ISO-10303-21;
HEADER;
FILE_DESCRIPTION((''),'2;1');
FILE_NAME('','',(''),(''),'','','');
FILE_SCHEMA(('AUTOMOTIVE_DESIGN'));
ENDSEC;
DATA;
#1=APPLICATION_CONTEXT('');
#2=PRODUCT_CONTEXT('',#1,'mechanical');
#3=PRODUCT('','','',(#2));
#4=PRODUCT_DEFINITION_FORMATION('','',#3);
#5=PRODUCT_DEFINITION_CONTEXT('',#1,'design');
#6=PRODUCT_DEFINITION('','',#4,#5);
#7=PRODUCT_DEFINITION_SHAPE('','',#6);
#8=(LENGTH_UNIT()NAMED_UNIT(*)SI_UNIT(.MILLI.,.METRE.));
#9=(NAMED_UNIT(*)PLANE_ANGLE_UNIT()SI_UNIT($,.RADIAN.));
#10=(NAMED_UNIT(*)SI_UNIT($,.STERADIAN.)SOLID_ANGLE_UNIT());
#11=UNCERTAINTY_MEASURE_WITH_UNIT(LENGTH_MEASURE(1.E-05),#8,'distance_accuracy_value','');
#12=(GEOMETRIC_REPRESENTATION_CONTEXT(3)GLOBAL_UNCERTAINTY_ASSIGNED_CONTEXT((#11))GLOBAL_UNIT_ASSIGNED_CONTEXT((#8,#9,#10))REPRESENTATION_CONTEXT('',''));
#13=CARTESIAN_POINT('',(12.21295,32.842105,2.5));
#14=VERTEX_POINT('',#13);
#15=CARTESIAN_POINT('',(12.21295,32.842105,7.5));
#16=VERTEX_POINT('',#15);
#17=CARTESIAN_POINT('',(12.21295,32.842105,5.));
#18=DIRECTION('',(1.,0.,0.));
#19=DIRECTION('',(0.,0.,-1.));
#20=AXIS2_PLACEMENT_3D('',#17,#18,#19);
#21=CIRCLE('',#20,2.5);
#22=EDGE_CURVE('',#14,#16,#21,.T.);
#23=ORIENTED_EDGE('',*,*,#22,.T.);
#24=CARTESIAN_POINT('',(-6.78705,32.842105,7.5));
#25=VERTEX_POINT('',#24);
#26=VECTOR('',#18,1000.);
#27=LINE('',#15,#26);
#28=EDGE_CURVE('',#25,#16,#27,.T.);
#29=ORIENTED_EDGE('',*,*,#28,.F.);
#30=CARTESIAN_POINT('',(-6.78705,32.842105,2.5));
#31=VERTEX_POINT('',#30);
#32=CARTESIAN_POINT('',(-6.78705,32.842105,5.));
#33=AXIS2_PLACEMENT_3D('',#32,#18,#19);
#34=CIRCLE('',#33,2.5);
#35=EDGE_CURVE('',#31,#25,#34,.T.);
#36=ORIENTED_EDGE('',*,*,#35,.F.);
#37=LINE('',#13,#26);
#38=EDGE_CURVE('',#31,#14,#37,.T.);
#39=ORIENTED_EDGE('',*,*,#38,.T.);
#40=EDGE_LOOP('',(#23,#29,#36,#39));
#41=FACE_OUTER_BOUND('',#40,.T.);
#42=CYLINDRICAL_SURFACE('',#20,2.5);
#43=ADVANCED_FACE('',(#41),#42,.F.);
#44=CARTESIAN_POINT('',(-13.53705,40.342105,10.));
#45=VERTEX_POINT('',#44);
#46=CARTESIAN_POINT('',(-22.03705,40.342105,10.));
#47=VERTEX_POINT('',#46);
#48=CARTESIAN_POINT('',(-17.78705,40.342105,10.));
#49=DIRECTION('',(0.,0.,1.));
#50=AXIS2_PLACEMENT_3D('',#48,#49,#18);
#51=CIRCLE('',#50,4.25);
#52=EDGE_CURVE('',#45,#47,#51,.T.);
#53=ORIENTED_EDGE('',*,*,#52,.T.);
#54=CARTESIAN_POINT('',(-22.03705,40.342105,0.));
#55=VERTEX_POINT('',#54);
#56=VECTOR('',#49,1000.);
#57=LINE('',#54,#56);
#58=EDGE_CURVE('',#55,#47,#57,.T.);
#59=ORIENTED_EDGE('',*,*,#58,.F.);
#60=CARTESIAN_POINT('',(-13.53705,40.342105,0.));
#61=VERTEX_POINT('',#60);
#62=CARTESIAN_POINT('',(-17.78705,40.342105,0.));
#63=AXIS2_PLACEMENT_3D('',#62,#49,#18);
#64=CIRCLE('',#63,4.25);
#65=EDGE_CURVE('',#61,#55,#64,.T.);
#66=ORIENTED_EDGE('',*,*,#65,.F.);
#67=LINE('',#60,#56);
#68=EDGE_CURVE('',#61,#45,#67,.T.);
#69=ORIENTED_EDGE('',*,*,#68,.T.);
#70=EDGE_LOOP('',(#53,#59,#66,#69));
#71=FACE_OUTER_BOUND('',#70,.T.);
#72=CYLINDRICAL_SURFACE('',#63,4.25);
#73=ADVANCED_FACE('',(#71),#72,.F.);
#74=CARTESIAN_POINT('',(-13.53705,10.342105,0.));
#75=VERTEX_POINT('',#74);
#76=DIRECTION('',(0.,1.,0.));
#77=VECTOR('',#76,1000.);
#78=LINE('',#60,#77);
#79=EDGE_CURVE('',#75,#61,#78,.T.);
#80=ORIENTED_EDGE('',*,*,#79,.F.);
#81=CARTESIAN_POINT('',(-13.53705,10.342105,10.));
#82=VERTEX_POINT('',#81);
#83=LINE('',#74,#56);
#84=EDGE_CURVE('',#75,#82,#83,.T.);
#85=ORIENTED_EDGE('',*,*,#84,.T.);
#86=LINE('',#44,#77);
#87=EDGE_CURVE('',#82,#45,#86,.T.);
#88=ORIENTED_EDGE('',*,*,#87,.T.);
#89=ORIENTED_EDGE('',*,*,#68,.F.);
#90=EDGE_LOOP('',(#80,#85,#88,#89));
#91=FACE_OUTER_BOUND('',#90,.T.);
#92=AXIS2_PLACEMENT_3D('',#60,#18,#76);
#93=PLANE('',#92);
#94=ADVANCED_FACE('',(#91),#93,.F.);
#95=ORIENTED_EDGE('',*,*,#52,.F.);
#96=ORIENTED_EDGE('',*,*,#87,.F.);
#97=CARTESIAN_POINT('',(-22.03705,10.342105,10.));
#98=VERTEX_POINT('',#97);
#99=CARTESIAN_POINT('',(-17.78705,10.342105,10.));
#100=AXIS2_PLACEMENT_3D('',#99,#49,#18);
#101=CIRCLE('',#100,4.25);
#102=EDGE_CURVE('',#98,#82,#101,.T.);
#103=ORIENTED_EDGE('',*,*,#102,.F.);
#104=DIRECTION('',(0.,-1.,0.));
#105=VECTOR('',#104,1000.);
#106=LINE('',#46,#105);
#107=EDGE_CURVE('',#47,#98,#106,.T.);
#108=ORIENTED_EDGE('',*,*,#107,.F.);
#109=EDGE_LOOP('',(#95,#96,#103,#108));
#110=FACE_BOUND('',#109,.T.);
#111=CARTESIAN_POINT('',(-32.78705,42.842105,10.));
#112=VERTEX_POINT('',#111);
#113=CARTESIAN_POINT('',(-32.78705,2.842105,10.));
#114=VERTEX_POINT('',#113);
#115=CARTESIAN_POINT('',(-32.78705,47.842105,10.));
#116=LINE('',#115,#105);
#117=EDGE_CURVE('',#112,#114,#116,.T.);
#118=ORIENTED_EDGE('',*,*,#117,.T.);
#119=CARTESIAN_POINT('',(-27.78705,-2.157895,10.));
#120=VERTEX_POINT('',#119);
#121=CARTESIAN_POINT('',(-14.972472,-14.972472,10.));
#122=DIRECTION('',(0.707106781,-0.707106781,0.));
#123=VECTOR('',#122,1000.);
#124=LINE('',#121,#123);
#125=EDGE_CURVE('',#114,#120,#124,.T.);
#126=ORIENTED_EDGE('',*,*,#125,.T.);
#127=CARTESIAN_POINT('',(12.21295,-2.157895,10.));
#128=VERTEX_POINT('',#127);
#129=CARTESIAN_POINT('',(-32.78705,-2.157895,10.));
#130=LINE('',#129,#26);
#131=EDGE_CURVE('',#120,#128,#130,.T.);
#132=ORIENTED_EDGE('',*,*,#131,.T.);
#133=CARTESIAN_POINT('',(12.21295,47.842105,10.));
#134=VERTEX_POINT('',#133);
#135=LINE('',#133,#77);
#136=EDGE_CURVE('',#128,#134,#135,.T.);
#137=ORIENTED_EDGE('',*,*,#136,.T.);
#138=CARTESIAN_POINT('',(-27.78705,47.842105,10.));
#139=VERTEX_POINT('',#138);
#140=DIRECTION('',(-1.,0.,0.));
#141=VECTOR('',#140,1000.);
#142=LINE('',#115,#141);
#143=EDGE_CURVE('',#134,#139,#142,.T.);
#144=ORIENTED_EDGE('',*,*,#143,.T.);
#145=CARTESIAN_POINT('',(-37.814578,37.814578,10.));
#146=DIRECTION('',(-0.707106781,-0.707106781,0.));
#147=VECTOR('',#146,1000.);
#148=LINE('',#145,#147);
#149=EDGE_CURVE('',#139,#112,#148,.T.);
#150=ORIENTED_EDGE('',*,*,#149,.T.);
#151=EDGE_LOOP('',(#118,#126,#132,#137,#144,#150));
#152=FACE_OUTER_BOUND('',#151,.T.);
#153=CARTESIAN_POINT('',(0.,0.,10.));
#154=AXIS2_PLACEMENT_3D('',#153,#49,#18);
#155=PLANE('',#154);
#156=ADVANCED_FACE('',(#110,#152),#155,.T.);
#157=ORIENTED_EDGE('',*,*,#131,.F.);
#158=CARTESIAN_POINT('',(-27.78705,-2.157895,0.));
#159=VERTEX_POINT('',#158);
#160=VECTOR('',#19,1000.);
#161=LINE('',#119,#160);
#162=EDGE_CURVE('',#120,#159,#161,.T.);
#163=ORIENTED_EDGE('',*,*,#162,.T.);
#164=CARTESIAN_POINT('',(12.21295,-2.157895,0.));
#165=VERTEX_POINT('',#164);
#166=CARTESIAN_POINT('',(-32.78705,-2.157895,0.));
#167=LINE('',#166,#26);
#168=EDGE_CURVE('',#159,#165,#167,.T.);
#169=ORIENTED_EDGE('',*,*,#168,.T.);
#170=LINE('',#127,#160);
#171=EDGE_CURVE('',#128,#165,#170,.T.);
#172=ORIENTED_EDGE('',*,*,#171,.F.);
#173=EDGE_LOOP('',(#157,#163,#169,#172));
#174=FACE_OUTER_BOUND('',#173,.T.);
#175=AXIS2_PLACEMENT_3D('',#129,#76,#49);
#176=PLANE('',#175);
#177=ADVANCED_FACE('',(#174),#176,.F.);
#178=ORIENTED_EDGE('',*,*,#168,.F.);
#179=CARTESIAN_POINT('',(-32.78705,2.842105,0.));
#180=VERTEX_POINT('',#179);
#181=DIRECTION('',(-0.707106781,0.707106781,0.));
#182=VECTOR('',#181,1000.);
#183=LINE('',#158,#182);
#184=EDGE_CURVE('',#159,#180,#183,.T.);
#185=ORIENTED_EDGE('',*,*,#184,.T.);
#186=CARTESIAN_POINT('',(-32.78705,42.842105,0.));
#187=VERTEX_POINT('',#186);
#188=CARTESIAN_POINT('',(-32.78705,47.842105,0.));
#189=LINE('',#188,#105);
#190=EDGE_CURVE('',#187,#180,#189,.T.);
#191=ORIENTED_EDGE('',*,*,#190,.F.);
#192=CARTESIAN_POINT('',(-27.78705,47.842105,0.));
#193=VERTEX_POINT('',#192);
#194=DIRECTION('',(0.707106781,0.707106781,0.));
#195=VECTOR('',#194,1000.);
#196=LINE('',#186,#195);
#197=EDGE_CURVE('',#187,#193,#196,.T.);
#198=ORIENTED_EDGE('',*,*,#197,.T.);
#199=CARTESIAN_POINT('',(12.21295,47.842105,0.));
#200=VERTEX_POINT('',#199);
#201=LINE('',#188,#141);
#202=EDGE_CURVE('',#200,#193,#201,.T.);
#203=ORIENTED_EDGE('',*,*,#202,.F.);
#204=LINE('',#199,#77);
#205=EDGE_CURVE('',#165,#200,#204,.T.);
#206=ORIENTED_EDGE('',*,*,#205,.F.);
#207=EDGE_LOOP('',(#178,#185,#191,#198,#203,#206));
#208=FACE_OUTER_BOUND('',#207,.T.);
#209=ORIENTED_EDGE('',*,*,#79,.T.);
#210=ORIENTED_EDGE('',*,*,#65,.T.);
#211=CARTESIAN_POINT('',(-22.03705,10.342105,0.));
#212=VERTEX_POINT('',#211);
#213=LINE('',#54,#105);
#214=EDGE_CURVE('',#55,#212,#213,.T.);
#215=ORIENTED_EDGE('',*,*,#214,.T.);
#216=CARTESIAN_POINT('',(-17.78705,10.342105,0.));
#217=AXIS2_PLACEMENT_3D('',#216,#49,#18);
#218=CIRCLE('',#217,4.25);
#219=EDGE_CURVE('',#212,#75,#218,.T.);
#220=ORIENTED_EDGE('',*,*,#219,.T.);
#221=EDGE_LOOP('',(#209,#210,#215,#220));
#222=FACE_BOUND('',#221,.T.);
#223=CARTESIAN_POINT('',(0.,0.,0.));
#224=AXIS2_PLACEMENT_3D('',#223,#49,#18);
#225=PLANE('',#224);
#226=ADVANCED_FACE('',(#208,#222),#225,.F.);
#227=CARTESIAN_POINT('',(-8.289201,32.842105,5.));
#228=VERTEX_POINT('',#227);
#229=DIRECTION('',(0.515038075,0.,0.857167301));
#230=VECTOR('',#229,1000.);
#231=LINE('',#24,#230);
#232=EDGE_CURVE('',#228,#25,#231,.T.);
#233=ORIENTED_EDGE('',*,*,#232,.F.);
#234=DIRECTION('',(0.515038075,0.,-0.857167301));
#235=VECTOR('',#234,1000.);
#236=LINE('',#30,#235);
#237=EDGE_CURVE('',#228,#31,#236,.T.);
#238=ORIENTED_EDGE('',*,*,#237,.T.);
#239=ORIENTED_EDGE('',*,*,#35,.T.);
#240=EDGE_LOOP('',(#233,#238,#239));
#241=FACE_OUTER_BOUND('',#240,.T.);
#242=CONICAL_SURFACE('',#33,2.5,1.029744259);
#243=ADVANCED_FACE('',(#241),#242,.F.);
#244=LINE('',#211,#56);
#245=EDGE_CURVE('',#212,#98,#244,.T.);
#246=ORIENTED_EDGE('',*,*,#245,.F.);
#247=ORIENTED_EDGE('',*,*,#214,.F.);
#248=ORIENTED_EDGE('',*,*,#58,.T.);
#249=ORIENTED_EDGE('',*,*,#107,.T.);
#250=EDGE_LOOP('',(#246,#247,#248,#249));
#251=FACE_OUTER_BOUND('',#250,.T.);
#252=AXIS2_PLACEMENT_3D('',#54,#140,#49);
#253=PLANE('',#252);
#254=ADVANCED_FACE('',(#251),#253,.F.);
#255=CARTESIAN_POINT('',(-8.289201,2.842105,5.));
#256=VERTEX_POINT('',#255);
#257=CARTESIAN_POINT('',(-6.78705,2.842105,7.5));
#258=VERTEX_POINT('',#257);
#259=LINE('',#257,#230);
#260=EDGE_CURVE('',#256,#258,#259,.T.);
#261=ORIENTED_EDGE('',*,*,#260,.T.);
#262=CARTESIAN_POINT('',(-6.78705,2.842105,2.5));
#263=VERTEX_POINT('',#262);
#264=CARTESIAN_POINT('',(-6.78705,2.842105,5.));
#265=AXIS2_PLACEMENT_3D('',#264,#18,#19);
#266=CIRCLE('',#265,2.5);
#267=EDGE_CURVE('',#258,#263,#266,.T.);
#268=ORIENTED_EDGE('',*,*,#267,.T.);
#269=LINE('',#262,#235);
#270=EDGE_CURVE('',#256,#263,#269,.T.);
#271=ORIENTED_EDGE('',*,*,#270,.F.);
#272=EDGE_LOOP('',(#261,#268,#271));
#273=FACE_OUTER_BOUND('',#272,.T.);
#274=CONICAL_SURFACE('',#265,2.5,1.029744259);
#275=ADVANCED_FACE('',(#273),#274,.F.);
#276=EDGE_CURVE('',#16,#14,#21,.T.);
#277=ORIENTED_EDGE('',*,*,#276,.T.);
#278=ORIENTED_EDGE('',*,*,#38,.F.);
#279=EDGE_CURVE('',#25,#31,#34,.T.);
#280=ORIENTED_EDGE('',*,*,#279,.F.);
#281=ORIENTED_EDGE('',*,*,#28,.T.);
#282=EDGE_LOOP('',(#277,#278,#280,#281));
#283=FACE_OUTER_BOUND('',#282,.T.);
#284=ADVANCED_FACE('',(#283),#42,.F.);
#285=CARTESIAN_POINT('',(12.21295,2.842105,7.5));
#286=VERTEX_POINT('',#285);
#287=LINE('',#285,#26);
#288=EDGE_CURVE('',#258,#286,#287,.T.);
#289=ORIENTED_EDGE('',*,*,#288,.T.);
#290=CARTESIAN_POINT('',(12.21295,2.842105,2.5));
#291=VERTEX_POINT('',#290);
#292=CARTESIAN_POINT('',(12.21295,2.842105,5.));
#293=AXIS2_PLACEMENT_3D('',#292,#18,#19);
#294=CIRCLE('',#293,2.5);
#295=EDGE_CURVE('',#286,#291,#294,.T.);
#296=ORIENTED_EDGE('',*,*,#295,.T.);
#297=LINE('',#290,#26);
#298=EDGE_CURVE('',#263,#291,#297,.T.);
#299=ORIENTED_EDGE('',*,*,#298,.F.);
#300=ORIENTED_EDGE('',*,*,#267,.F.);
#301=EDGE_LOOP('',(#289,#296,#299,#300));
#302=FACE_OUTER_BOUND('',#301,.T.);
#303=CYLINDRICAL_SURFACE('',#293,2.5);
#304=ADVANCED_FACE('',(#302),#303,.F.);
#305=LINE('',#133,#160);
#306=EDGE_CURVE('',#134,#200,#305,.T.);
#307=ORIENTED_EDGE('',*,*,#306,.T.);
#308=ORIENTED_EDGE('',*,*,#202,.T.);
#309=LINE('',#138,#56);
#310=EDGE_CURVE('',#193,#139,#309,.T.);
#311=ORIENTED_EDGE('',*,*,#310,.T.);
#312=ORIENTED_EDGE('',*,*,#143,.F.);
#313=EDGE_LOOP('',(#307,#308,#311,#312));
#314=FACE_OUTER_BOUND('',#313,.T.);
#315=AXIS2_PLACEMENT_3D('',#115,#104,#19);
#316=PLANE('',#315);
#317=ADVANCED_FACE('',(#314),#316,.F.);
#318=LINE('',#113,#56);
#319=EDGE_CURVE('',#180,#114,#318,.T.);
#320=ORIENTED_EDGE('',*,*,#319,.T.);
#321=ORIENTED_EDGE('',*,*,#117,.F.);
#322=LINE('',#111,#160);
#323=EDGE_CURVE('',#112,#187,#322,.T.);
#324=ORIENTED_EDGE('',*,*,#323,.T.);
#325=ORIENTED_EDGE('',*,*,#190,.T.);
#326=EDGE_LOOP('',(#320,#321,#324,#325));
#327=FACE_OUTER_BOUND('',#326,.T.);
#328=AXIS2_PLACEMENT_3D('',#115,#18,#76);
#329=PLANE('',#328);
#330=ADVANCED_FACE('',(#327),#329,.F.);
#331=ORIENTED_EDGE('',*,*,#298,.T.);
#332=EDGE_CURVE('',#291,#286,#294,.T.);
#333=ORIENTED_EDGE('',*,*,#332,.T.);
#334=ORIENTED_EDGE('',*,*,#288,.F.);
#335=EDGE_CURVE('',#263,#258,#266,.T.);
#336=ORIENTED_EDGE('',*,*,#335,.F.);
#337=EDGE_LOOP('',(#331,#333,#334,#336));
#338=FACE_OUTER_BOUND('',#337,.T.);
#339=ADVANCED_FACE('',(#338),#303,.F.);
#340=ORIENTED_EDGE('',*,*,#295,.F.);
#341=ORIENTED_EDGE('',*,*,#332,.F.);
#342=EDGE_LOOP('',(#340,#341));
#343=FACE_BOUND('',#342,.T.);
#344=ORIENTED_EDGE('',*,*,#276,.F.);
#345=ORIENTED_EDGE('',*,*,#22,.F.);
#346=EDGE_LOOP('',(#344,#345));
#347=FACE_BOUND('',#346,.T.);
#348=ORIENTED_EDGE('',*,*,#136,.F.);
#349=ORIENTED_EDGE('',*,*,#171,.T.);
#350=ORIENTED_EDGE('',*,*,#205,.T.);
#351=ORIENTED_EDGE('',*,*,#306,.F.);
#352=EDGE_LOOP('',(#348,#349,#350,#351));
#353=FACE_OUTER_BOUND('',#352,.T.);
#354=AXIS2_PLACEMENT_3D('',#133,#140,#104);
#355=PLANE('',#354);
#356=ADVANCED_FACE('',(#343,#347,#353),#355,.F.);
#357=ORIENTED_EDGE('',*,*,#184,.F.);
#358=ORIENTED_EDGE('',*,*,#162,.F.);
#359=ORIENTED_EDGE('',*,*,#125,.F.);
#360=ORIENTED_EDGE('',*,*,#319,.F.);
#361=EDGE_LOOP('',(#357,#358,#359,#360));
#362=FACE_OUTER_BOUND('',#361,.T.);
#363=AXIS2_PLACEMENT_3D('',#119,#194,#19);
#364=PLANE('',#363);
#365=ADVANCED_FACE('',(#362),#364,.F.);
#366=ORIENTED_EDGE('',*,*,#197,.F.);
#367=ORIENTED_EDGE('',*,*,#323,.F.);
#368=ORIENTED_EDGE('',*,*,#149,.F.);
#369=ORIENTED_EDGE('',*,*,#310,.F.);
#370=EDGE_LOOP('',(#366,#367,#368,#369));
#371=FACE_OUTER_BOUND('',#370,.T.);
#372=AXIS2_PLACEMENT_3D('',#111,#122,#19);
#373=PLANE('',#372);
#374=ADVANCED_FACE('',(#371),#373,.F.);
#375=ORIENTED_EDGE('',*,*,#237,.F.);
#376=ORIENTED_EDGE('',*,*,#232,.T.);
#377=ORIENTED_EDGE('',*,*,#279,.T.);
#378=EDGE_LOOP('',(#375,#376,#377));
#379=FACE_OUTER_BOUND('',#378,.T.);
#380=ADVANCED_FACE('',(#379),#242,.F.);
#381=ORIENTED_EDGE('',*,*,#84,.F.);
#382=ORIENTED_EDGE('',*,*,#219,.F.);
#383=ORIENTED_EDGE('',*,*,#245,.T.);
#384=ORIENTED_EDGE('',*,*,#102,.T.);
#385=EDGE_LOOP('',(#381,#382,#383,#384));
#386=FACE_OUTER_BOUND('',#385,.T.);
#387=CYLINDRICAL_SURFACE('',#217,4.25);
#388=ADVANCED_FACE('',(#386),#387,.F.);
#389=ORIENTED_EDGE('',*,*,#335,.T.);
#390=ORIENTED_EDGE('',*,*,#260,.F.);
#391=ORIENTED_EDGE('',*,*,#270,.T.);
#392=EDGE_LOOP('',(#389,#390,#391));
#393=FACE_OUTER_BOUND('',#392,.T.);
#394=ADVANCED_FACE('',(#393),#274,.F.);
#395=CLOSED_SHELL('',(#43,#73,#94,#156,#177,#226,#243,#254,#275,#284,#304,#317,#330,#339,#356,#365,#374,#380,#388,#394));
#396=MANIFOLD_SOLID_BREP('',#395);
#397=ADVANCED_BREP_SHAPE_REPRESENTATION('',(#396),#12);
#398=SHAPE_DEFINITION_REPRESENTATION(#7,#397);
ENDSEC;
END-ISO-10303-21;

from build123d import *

# Parameters (mm, degrees)
SKETCH1_W             = 45
SKETCH1_H             = 50
BOSS_EXTRUDE1_DEPTH   = 10
CUT_EXTRUDE1_DEPTH    = 59.854546763
CHAMFER1_SIZE         = 5
M6_TAPPED_HOLE1_D     = 5
M6_TAPPED_HOLE1_DEPTH = 19
M6_TAPPED_HOLE1_TIP   = 1.502151548


with BuildPart() as part:
    # Sketch1 → Boss-Extrude1 (new body)
    with BuildSketch(Plane.XY):
        with Locations((-10.287049861, 22.842105263)):
            Rectangle(SKETCH1_W, SKETCH1_H)
    extrude(amount=BOSS_EXTRUDE1_DEPTH)

    # Sketch2 → Cut-Extrude1 (cut, through all)
    with BuildSketch(Plane.XY.offset(10)):
        with BuildLine():
            Line((-13.537049861, 40.342105263), (-13.537049861, 10.342105263))
            ThreePointArc((-13.537049861, 10.342105263), (-17.787049861, 6.092105263), (-22.037049861, 10.342105263))
            Line((-22.037049861, 10.342105263), (-22.037049861, 40.342105263))
            ThreePointArc((-22.037049861, 40.342105263), (-17.787049861, 44.592105263), (-13.537049861, 40.342105263))
        make_face()
    extrude(amount=-CUT_EXTRUDE1_DEPTH, mode=Mode.SUBTRACT)

    # Chamfer1
    chamfer1_edges = [part.edges().sort_by_distance(p)[0] for p in [
        (-32.787049861, 47.842105263, 5),
        (-32.787049861, -2.157894737, 5),
    ]]
    chamfer(chamfer1_edges, length=CHAMFER1_SIZE)

    # M6 Tapped Hole1
    with Locations(Plane(origin=(12.212950139, 0, 0), x_dir=(0, 0, -1), z_dir=(1, 0, 0))):
        with Locations((-5, 32.842105263), (-5, 2.842105263)):
            Hole(M6_TAPPED_HOLE1_D / 2, depth=M6_TAPPED_HOLE1_DEPTH)
            with Locations((0, 0, -(M6_TAPPED_HOLE1_DEPTH + M6_TAPPED_HOLE1_TIP / 2))):  # 118° drill point
                Cone(0, M6_TAPPED_HOLE1_D / 2, M6_TAPPED_HOLE1_TIP, mode=Mode.SUBTRACT)


solid = part.part
